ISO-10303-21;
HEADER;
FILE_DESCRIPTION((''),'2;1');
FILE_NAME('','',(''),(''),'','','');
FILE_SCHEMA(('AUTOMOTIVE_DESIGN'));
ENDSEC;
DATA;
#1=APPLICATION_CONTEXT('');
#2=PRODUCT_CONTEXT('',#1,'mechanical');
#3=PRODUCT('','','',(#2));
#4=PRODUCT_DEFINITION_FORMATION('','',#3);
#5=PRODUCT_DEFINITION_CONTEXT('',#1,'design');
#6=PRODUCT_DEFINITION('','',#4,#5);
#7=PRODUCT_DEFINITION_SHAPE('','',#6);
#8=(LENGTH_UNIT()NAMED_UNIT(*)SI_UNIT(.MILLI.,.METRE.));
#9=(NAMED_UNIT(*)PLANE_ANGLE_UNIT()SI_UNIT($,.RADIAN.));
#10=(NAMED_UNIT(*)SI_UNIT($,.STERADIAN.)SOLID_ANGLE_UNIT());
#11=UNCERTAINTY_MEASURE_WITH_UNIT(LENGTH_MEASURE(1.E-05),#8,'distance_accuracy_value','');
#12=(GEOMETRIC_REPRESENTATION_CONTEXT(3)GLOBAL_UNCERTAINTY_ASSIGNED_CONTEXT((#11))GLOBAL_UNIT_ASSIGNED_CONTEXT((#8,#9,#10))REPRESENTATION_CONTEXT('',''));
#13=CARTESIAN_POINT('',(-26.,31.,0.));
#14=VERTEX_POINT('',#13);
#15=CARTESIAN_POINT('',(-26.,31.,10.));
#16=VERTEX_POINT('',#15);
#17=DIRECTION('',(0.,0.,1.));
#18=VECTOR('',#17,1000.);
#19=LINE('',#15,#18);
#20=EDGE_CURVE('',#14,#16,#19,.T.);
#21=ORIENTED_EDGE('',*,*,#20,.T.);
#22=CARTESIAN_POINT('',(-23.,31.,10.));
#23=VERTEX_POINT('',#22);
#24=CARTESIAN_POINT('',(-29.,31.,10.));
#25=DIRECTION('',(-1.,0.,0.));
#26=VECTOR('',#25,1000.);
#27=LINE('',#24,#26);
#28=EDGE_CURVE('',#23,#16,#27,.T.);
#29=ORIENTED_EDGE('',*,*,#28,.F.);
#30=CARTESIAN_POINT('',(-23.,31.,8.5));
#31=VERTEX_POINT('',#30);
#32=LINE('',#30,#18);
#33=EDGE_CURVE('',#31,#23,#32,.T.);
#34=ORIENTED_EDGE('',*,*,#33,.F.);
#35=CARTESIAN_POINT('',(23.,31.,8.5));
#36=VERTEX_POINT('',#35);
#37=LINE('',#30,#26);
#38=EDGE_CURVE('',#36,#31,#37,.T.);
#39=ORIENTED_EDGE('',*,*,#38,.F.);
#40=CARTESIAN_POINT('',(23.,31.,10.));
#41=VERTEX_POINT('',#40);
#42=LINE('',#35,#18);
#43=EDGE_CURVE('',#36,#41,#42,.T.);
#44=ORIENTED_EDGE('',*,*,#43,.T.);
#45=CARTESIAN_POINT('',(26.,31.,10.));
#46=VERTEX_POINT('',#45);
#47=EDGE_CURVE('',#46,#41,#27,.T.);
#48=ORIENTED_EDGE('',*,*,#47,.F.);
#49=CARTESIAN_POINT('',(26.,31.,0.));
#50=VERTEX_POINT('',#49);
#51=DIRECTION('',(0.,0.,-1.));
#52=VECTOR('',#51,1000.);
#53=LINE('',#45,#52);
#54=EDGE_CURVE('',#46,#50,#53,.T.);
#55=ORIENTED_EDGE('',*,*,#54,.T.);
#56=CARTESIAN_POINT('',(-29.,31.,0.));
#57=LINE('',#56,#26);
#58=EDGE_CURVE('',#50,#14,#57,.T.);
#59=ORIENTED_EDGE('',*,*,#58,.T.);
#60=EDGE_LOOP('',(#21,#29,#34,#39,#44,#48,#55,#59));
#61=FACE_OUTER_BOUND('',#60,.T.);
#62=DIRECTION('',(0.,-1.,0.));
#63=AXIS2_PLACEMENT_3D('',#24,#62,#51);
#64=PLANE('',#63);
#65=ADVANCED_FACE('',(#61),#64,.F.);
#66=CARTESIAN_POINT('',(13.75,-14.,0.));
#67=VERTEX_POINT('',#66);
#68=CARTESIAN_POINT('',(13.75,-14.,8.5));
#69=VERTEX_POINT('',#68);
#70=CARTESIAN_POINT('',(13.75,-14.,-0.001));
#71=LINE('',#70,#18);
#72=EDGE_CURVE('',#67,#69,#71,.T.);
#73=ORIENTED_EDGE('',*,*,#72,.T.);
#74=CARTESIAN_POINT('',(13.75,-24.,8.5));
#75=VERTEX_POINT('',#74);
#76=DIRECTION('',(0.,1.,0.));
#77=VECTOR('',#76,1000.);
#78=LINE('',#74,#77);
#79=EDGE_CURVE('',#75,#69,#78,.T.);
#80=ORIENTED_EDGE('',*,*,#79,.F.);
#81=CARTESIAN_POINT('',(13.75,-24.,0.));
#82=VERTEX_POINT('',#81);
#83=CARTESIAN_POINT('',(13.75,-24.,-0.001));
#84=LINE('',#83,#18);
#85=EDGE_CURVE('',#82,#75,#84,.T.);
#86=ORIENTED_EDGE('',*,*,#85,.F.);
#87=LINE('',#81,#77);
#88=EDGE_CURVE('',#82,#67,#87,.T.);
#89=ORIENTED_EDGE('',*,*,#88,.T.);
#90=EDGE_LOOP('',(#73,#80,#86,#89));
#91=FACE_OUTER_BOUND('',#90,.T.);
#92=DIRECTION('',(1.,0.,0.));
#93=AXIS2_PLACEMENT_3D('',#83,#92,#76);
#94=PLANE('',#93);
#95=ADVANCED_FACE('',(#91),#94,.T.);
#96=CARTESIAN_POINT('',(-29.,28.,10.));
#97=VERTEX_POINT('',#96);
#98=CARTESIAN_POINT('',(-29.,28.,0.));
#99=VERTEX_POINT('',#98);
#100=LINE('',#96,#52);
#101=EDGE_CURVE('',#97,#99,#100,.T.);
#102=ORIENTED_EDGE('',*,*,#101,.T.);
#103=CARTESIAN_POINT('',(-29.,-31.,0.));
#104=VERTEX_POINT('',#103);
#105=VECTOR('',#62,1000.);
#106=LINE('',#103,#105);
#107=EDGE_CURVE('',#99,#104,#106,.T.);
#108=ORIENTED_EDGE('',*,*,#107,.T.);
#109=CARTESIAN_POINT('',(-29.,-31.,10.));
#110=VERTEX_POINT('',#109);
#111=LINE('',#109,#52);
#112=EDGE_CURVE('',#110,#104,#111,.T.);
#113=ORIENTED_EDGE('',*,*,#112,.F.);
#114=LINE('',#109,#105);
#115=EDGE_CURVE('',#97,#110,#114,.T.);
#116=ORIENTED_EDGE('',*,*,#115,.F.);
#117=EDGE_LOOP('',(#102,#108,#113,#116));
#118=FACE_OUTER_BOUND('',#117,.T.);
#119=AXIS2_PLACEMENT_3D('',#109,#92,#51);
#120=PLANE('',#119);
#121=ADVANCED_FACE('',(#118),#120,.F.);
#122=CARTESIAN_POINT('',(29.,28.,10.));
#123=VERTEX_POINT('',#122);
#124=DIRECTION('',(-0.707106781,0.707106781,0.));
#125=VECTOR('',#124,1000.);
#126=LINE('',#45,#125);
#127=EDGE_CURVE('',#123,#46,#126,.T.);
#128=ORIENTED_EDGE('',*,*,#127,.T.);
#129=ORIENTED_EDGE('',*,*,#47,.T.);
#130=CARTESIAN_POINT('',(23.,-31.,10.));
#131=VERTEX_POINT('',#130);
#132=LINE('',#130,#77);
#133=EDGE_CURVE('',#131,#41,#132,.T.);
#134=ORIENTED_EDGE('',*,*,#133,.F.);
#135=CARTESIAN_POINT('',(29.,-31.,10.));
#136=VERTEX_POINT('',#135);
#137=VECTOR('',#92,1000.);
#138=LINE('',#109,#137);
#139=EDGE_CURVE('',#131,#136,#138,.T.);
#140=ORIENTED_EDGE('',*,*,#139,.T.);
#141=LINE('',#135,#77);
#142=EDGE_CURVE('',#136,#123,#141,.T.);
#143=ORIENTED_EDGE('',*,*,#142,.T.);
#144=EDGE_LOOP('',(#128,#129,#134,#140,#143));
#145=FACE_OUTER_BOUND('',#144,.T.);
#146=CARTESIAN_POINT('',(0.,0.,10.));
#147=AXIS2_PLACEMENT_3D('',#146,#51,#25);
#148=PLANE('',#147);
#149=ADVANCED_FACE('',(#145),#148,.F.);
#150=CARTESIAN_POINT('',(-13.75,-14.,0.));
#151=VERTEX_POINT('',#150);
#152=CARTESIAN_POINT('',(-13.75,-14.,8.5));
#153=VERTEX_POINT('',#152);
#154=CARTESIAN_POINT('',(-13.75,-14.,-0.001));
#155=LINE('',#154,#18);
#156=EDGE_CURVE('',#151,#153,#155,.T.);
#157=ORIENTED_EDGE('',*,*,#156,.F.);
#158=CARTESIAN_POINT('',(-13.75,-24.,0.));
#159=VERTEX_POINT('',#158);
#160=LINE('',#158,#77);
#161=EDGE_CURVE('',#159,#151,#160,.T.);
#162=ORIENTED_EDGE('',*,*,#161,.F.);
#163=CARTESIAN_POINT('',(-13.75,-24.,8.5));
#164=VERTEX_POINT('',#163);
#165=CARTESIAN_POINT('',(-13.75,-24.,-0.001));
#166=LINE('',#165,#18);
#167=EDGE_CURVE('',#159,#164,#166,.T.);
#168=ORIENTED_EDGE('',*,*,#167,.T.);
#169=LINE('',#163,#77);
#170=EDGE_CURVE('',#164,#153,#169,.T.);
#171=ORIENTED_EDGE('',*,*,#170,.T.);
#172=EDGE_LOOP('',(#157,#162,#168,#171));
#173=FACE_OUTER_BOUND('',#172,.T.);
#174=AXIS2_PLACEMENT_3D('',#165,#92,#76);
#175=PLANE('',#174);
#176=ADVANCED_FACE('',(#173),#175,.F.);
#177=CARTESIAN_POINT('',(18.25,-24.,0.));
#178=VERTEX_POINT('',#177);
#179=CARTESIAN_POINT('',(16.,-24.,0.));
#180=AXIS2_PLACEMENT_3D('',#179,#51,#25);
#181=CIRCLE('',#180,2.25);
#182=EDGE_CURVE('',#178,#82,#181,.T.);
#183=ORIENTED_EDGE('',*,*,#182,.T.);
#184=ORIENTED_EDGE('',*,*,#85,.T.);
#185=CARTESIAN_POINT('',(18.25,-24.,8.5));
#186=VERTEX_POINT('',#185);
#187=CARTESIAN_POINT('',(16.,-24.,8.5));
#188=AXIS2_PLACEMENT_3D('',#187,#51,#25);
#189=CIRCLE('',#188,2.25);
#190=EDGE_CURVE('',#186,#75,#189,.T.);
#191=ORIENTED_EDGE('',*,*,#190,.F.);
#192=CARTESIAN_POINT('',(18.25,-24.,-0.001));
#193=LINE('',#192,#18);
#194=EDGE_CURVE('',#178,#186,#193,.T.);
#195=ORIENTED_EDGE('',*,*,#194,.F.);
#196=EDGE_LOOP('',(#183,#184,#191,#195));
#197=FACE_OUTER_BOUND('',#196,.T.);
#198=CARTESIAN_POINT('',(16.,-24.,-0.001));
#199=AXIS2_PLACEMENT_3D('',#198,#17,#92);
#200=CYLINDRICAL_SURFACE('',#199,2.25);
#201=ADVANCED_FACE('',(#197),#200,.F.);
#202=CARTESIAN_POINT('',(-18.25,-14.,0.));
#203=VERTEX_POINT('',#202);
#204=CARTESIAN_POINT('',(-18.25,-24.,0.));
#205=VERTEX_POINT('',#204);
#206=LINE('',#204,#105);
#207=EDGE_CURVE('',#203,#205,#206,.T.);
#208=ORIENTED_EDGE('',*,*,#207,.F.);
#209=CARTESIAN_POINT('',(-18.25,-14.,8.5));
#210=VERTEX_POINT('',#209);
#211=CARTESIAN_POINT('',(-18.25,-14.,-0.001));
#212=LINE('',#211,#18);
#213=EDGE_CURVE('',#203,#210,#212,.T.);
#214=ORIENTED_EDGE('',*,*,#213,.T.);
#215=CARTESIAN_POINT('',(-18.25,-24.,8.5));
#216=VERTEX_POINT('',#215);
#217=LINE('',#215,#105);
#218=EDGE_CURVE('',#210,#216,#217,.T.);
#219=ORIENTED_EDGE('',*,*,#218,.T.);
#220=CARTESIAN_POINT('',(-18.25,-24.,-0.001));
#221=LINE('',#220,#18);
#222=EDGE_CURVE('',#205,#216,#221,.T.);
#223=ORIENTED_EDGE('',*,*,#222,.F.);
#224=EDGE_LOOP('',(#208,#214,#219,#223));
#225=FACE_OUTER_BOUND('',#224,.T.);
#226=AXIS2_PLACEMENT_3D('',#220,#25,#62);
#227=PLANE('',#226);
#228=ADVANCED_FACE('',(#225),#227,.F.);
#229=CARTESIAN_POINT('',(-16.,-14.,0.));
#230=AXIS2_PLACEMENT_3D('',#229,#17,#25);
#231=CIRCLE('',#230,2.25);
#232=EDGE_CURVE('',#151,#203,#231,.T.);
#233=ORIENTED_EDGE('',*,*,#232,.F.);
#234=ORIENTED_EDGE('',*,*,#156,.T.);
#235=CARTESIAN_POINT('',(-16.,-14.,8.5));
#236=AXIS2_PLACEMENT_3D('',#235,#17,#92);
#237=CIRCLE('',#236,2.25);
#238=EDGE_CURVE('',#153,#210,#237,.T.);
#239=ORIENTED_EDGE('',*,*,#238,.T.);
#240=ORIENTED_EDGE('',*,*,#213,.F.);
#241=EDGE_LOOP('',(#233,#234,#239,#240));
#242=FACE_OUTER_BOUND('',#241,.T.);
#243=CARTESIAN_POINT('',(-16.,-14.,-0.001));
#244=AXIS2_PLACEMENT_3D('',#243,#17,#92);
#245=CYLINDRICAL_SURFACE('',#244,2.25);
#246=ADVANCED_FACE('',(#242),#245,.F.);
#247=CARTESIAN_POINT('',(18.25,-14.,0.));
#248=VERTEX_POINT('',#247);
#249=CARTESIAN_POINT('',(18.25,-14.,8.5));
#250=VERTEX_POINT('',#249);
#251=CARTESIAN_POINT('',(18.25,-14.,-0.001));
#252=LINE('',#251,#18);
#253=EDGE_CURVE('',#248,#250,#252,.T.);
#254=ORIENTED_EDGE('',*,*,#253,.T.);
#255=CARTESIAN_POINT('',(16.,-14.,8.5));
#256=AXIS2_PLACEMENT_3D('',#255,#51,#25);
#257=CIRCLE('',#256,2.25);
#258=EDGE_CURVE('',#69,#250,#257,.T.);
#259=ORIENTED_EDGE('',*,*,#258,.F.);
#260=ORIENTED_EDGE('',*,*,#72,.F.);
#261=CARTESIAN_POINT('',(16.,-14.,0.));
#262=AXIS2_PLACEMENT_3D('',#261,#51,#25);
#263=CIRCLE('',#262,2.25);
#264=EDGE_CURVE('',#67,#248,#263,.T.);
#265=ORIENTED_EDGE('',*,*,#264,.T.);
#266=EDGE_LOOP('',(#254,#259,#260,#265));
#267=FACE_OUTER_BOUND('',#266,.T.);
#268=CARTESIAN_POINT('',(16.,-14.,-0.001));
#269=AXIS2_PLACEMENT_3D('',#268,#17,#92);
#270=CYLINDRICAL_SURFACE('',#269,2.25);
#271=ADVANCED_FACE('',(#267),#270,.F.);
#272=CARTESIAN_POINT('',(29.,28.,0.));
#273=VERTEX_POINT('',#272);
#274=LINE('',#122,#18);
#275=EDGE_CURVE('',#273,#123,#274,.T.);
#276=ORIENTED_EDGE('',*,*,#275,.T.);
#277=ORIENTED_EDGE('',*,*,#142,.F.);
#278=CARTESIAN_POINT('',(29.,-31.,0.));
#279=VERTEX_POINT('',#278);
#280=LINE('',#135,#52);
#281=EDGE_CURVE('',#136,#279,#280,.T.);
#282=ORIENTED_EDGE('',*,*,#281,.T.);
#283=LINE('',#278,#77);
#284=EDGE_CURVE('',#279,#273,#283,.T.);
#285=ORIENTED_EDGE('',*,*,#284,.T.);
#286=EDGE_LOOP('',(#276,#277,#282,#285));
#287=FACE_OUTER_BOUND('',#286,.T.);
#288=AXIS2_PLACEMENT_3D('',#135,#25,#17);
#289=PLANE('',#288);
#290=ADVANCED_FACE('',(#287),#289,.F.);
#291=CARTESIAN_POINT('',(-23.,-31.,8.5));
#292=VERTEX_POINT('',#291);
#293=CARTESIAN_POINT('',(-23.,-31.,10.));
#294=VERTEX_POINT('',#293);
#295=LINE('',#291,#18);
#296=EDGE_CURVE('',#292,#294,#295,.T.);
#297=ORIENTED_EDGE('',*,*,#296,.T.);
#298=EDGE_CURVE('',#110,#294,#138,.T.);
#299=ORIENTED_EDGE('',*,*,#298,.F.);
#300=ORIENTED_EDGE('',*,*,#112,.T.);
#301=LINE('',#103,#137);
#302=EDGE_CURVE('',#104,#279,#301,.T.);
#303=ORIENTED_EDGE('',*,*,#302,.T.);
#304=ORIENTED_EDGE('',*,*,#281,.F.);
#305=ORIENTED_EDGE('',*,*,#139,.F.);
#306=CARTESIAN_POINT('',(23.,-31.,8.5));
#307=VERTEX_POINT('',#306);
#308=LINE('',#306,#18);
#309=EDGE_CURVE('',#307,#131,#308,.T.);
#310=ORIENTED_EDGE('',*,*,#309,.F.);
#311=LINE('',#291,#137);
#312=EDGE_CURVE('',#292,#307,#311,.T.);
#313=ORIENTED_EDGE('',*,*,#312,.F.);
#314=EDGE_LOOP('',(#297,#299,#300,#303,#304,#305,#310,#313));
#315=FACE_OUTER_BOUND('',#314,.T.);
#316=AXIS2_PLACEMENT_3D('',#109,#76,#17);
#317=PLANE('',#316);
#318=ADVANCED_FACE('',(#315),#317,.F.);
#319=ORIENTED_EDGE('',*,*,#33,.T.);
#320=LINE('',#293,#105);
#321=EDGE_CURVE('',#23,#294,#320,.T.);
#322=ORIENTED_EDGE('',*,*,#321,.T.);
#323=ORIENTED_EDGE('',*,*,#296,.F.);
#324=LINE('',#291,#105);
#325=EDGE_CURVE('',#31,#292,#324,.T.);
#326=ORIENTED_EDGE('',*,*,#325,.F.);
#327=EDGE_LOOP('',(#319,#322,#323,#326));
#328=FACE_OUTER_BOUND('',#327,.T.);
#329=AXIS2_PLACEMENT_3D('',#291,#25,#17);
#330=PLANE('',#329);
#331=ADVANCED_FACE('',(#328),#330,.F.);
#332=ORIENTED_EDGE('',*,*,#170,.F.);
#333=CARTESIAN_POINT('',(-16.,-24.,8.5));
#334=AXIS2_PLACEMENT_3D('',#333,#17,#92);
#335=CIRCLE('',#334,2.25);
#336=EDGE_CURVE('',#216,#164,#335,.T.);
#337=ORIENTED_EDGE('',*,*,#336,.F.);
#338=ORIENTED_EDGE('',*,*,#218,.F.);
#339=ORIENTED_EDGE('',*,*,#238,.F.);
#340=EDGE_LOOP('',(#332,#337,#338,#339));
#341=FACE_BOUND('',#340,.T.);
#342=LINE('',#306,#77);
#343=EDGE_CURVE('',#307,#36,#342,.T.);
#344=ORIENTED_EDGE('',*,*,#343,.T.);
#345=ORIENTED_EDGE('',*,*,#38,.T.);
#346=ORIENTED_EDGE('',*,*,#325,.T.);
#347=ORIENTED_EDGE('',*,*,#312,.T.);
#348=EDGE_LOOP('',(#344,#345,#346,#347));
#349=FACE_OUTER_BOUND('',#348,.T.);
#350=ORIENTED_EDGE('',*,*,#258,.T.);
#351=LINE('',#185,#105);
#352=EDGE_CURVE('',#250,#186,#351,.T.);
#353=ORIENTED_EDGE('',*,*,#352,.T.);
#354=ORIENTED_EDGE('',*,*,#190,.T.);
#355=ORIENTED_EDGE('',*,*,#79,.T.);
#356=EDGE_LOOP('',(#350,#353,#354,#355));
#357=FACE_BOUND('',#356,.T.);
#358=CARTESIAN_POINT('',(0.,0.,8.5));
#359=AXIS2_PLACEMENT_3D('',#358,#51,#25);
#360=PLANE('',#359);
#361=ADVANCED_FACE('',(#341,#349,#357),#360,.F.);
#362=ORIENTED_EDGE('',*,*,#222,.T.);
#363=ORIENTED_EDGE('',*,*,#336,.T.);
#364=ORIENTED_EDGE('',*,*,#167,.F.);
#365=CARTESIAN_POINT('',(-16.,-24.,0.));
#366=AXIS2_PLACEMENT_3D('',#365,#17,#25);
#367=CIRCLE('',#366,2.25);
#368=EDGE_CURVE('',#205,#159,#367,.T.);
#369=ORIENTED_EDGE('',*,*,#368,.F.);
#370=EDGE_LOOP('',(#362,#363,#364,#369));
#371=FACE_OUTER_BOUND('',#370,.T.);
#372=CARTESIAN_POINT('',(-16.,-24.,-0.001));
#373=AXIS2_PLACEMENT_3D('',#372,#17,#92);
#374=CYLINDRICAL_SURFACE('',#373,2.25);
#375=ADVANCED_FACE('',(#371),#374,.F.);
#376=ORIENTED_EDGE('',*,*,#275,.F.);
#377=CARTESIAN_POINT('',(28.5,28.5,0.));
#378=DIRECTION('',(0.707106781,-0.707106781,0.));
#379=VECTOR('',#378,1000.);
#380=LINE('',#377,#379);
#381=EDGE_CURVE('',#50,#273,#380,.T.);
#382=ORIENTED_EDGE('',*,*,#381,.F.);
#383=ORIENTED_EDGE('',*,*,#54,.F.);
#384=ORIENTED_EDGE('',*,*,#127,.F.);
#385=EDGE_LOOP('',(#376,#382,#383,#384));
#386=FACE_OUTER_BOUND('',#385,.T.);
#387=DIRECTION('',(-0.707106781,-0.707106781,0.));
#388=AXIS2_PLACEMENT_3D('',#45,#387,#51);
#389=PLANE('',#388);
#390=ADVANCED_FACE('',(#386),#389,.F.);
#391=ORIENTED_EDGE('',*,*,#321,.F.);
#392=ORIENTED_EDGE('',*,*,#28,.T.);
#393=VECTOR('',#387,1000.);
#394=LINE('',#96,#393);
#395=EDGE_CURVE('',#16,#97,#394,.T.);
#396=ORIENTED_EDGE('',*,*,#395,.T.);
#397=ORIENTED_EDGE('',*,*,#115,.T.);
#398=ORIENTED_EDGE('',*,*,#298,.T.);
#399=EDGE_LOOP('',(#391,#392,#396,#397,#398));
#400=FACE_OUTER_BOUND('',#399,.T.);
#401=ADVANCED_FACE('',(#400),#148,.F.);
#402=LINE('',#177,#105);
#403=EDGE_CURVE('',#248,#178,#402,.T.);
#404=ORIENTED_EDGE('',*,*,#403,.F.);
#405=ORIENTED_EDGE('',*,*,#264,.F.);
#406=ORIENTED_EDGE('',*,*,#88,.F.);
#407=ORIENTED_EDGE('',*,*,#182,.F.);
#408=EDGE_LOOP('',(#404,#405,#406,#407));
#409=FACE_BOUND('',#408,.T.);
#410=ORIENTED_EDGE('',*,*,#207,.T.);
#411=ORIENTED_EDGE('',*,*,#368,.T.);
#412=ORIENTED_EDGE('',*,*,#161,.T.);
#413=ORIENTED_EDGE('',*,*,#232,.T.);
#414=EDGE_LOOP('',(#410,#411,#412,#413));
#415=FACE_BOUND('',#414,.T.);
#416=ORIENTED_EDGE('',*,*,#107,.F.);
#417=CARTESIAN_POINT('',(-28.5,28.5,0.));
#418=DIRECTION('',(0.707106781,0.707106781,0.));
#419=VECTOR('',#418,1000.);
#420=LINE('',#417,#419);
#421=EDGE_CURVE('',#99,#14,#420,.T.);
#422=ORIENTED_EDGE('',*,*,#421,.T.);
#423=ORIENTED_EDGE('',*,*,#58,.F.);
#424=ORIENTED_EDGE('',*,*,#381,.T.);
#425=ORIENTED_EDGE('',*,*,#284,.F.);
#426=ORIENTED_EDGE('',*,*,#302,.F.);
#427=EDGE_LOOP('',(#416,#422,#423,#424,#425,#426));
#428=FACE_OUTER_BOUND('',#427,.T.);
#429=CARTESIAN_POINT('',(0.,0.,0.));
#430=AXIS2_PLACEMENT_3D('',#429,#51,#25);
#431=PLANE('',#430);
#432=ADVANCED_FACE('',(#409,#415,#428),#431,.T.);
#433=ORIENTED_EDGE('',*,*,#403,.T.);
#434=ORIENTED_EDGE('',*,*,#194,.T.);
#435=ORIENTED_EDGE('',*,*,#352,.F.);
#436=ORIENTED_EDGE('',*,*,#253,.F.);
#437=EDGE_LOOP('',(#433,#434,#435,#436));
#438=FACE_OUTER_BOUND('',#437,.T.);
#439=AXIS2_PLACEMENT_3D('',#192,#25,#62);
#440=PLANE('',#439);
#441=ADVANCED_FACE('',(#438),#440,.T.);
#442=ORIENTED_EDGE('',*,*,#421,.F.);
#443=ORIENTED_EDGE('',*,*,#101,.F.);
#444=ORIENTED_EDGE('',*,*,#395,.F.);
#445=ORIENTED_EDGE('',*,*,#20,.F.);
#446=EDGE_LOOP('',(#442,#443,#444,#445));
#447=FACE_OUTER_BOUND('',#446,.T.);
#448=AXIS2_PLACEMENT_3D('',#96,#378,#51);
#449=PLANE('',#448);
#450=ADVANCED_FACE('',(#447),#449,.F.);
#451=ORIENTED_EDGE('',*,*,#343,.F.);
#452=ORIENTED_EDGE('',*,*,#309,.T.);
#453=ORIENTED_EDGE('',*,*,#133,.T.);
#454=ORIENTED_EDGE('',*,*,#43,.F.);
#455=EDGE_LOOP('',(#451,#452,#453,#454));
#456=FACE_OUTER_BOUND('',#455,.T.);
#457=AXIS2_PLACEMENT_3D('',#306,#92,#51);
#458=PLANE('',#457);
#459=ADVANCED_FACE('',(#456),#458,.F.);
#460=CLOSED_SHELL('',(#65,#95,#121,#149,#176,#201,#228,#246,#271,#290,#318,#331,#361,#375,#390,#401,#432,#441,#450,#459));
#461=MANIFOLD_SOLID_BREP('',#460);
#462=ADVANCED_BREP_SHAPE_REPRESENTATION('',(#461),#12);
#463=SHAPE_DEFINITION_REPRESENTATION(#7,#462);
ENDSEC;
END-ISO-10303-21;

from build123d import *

# Parameters (mm, degrees)
SKETCH_1_W          = 58
SKETCH_1_H          = 62
EXTRUDE_1_DEPTH     = 10
SKETCH_2_W          = 46
SKETCH_2_H          = 62
CUT_EXTRUDE_1_DEPTH = 1.5
CHAMFER_1_SIZE      = 3
CUT_EXTRUDE_2_REACH = 45.293


with BuildPart() as part:
    # 草图1 → 凸台-拉伸1 (new body)
    with BuildSketch(Plane.XY):
        Rectangle(SKETCH_1_W, SKETCH_1_H)
    extrude(amount=EXTRUDE_1_DEPTH)

    # 草图2 → 切除-拉伸1 (cut)
    with BuildSketch(Plane.XY.offset(10)):
        Rectangle(SKETCH_2_W, SKETCH_2_H)
    extrude(amount=-CUT_EXTRUDE_1_DEPTH, mode=Mode.SUBTRACT)

    # 倒角1
    chamfer_1_edges = [part.edges().sort_by_distance(p)[0] for p in [
        (-29, 31, 5),
        (29, 31, 5),
    ]]
    chamfer(chamfer_1_edges, length=CHAMFER_1_SIZE)

    # 草图3 → 切除-拉伸2 (cut, up to next)
    with BuildSketch(Plane.XY.offset(8.5), mode=Mode.PRIVATE) as cut_extrude_2_sk1:
        with BuildLine():
            Line((-18.25, -24), (-18.25, -14))
            ThreePointArc((-18.25, -14), (-16, -11.75), (-13.75, -14))
            Line((-13.75, -14), (-13.75, -24))
            ThreePointArc((-13.75, -24), (-16, -26.25), (-18.25, -24))
        make_face()
    cut_extrude_2_tool1 = extrude(cut_extrude_2_sk1.sketch, amount=-CUT_EXTRUDE_2_REACH, mode=Mode.PRIVATE) & part.part
    cut_extrude_2 = cut_extrude_2_tool1.solids().sort_by_distance((-16, -19, 8.5))[0]
    add(cut_extrude_2, mode=Mode.SUBTRACT)

    # 镜向1: 切除-拉伸2 across plane
    add(cut_extrude_2.mirror(Plane(origin=(0, 0, 0), x_dir=(0, 0, 1), z_dir=(1, 0, 0))), mode=Mode.SUBTRACT)


solid = part.part
